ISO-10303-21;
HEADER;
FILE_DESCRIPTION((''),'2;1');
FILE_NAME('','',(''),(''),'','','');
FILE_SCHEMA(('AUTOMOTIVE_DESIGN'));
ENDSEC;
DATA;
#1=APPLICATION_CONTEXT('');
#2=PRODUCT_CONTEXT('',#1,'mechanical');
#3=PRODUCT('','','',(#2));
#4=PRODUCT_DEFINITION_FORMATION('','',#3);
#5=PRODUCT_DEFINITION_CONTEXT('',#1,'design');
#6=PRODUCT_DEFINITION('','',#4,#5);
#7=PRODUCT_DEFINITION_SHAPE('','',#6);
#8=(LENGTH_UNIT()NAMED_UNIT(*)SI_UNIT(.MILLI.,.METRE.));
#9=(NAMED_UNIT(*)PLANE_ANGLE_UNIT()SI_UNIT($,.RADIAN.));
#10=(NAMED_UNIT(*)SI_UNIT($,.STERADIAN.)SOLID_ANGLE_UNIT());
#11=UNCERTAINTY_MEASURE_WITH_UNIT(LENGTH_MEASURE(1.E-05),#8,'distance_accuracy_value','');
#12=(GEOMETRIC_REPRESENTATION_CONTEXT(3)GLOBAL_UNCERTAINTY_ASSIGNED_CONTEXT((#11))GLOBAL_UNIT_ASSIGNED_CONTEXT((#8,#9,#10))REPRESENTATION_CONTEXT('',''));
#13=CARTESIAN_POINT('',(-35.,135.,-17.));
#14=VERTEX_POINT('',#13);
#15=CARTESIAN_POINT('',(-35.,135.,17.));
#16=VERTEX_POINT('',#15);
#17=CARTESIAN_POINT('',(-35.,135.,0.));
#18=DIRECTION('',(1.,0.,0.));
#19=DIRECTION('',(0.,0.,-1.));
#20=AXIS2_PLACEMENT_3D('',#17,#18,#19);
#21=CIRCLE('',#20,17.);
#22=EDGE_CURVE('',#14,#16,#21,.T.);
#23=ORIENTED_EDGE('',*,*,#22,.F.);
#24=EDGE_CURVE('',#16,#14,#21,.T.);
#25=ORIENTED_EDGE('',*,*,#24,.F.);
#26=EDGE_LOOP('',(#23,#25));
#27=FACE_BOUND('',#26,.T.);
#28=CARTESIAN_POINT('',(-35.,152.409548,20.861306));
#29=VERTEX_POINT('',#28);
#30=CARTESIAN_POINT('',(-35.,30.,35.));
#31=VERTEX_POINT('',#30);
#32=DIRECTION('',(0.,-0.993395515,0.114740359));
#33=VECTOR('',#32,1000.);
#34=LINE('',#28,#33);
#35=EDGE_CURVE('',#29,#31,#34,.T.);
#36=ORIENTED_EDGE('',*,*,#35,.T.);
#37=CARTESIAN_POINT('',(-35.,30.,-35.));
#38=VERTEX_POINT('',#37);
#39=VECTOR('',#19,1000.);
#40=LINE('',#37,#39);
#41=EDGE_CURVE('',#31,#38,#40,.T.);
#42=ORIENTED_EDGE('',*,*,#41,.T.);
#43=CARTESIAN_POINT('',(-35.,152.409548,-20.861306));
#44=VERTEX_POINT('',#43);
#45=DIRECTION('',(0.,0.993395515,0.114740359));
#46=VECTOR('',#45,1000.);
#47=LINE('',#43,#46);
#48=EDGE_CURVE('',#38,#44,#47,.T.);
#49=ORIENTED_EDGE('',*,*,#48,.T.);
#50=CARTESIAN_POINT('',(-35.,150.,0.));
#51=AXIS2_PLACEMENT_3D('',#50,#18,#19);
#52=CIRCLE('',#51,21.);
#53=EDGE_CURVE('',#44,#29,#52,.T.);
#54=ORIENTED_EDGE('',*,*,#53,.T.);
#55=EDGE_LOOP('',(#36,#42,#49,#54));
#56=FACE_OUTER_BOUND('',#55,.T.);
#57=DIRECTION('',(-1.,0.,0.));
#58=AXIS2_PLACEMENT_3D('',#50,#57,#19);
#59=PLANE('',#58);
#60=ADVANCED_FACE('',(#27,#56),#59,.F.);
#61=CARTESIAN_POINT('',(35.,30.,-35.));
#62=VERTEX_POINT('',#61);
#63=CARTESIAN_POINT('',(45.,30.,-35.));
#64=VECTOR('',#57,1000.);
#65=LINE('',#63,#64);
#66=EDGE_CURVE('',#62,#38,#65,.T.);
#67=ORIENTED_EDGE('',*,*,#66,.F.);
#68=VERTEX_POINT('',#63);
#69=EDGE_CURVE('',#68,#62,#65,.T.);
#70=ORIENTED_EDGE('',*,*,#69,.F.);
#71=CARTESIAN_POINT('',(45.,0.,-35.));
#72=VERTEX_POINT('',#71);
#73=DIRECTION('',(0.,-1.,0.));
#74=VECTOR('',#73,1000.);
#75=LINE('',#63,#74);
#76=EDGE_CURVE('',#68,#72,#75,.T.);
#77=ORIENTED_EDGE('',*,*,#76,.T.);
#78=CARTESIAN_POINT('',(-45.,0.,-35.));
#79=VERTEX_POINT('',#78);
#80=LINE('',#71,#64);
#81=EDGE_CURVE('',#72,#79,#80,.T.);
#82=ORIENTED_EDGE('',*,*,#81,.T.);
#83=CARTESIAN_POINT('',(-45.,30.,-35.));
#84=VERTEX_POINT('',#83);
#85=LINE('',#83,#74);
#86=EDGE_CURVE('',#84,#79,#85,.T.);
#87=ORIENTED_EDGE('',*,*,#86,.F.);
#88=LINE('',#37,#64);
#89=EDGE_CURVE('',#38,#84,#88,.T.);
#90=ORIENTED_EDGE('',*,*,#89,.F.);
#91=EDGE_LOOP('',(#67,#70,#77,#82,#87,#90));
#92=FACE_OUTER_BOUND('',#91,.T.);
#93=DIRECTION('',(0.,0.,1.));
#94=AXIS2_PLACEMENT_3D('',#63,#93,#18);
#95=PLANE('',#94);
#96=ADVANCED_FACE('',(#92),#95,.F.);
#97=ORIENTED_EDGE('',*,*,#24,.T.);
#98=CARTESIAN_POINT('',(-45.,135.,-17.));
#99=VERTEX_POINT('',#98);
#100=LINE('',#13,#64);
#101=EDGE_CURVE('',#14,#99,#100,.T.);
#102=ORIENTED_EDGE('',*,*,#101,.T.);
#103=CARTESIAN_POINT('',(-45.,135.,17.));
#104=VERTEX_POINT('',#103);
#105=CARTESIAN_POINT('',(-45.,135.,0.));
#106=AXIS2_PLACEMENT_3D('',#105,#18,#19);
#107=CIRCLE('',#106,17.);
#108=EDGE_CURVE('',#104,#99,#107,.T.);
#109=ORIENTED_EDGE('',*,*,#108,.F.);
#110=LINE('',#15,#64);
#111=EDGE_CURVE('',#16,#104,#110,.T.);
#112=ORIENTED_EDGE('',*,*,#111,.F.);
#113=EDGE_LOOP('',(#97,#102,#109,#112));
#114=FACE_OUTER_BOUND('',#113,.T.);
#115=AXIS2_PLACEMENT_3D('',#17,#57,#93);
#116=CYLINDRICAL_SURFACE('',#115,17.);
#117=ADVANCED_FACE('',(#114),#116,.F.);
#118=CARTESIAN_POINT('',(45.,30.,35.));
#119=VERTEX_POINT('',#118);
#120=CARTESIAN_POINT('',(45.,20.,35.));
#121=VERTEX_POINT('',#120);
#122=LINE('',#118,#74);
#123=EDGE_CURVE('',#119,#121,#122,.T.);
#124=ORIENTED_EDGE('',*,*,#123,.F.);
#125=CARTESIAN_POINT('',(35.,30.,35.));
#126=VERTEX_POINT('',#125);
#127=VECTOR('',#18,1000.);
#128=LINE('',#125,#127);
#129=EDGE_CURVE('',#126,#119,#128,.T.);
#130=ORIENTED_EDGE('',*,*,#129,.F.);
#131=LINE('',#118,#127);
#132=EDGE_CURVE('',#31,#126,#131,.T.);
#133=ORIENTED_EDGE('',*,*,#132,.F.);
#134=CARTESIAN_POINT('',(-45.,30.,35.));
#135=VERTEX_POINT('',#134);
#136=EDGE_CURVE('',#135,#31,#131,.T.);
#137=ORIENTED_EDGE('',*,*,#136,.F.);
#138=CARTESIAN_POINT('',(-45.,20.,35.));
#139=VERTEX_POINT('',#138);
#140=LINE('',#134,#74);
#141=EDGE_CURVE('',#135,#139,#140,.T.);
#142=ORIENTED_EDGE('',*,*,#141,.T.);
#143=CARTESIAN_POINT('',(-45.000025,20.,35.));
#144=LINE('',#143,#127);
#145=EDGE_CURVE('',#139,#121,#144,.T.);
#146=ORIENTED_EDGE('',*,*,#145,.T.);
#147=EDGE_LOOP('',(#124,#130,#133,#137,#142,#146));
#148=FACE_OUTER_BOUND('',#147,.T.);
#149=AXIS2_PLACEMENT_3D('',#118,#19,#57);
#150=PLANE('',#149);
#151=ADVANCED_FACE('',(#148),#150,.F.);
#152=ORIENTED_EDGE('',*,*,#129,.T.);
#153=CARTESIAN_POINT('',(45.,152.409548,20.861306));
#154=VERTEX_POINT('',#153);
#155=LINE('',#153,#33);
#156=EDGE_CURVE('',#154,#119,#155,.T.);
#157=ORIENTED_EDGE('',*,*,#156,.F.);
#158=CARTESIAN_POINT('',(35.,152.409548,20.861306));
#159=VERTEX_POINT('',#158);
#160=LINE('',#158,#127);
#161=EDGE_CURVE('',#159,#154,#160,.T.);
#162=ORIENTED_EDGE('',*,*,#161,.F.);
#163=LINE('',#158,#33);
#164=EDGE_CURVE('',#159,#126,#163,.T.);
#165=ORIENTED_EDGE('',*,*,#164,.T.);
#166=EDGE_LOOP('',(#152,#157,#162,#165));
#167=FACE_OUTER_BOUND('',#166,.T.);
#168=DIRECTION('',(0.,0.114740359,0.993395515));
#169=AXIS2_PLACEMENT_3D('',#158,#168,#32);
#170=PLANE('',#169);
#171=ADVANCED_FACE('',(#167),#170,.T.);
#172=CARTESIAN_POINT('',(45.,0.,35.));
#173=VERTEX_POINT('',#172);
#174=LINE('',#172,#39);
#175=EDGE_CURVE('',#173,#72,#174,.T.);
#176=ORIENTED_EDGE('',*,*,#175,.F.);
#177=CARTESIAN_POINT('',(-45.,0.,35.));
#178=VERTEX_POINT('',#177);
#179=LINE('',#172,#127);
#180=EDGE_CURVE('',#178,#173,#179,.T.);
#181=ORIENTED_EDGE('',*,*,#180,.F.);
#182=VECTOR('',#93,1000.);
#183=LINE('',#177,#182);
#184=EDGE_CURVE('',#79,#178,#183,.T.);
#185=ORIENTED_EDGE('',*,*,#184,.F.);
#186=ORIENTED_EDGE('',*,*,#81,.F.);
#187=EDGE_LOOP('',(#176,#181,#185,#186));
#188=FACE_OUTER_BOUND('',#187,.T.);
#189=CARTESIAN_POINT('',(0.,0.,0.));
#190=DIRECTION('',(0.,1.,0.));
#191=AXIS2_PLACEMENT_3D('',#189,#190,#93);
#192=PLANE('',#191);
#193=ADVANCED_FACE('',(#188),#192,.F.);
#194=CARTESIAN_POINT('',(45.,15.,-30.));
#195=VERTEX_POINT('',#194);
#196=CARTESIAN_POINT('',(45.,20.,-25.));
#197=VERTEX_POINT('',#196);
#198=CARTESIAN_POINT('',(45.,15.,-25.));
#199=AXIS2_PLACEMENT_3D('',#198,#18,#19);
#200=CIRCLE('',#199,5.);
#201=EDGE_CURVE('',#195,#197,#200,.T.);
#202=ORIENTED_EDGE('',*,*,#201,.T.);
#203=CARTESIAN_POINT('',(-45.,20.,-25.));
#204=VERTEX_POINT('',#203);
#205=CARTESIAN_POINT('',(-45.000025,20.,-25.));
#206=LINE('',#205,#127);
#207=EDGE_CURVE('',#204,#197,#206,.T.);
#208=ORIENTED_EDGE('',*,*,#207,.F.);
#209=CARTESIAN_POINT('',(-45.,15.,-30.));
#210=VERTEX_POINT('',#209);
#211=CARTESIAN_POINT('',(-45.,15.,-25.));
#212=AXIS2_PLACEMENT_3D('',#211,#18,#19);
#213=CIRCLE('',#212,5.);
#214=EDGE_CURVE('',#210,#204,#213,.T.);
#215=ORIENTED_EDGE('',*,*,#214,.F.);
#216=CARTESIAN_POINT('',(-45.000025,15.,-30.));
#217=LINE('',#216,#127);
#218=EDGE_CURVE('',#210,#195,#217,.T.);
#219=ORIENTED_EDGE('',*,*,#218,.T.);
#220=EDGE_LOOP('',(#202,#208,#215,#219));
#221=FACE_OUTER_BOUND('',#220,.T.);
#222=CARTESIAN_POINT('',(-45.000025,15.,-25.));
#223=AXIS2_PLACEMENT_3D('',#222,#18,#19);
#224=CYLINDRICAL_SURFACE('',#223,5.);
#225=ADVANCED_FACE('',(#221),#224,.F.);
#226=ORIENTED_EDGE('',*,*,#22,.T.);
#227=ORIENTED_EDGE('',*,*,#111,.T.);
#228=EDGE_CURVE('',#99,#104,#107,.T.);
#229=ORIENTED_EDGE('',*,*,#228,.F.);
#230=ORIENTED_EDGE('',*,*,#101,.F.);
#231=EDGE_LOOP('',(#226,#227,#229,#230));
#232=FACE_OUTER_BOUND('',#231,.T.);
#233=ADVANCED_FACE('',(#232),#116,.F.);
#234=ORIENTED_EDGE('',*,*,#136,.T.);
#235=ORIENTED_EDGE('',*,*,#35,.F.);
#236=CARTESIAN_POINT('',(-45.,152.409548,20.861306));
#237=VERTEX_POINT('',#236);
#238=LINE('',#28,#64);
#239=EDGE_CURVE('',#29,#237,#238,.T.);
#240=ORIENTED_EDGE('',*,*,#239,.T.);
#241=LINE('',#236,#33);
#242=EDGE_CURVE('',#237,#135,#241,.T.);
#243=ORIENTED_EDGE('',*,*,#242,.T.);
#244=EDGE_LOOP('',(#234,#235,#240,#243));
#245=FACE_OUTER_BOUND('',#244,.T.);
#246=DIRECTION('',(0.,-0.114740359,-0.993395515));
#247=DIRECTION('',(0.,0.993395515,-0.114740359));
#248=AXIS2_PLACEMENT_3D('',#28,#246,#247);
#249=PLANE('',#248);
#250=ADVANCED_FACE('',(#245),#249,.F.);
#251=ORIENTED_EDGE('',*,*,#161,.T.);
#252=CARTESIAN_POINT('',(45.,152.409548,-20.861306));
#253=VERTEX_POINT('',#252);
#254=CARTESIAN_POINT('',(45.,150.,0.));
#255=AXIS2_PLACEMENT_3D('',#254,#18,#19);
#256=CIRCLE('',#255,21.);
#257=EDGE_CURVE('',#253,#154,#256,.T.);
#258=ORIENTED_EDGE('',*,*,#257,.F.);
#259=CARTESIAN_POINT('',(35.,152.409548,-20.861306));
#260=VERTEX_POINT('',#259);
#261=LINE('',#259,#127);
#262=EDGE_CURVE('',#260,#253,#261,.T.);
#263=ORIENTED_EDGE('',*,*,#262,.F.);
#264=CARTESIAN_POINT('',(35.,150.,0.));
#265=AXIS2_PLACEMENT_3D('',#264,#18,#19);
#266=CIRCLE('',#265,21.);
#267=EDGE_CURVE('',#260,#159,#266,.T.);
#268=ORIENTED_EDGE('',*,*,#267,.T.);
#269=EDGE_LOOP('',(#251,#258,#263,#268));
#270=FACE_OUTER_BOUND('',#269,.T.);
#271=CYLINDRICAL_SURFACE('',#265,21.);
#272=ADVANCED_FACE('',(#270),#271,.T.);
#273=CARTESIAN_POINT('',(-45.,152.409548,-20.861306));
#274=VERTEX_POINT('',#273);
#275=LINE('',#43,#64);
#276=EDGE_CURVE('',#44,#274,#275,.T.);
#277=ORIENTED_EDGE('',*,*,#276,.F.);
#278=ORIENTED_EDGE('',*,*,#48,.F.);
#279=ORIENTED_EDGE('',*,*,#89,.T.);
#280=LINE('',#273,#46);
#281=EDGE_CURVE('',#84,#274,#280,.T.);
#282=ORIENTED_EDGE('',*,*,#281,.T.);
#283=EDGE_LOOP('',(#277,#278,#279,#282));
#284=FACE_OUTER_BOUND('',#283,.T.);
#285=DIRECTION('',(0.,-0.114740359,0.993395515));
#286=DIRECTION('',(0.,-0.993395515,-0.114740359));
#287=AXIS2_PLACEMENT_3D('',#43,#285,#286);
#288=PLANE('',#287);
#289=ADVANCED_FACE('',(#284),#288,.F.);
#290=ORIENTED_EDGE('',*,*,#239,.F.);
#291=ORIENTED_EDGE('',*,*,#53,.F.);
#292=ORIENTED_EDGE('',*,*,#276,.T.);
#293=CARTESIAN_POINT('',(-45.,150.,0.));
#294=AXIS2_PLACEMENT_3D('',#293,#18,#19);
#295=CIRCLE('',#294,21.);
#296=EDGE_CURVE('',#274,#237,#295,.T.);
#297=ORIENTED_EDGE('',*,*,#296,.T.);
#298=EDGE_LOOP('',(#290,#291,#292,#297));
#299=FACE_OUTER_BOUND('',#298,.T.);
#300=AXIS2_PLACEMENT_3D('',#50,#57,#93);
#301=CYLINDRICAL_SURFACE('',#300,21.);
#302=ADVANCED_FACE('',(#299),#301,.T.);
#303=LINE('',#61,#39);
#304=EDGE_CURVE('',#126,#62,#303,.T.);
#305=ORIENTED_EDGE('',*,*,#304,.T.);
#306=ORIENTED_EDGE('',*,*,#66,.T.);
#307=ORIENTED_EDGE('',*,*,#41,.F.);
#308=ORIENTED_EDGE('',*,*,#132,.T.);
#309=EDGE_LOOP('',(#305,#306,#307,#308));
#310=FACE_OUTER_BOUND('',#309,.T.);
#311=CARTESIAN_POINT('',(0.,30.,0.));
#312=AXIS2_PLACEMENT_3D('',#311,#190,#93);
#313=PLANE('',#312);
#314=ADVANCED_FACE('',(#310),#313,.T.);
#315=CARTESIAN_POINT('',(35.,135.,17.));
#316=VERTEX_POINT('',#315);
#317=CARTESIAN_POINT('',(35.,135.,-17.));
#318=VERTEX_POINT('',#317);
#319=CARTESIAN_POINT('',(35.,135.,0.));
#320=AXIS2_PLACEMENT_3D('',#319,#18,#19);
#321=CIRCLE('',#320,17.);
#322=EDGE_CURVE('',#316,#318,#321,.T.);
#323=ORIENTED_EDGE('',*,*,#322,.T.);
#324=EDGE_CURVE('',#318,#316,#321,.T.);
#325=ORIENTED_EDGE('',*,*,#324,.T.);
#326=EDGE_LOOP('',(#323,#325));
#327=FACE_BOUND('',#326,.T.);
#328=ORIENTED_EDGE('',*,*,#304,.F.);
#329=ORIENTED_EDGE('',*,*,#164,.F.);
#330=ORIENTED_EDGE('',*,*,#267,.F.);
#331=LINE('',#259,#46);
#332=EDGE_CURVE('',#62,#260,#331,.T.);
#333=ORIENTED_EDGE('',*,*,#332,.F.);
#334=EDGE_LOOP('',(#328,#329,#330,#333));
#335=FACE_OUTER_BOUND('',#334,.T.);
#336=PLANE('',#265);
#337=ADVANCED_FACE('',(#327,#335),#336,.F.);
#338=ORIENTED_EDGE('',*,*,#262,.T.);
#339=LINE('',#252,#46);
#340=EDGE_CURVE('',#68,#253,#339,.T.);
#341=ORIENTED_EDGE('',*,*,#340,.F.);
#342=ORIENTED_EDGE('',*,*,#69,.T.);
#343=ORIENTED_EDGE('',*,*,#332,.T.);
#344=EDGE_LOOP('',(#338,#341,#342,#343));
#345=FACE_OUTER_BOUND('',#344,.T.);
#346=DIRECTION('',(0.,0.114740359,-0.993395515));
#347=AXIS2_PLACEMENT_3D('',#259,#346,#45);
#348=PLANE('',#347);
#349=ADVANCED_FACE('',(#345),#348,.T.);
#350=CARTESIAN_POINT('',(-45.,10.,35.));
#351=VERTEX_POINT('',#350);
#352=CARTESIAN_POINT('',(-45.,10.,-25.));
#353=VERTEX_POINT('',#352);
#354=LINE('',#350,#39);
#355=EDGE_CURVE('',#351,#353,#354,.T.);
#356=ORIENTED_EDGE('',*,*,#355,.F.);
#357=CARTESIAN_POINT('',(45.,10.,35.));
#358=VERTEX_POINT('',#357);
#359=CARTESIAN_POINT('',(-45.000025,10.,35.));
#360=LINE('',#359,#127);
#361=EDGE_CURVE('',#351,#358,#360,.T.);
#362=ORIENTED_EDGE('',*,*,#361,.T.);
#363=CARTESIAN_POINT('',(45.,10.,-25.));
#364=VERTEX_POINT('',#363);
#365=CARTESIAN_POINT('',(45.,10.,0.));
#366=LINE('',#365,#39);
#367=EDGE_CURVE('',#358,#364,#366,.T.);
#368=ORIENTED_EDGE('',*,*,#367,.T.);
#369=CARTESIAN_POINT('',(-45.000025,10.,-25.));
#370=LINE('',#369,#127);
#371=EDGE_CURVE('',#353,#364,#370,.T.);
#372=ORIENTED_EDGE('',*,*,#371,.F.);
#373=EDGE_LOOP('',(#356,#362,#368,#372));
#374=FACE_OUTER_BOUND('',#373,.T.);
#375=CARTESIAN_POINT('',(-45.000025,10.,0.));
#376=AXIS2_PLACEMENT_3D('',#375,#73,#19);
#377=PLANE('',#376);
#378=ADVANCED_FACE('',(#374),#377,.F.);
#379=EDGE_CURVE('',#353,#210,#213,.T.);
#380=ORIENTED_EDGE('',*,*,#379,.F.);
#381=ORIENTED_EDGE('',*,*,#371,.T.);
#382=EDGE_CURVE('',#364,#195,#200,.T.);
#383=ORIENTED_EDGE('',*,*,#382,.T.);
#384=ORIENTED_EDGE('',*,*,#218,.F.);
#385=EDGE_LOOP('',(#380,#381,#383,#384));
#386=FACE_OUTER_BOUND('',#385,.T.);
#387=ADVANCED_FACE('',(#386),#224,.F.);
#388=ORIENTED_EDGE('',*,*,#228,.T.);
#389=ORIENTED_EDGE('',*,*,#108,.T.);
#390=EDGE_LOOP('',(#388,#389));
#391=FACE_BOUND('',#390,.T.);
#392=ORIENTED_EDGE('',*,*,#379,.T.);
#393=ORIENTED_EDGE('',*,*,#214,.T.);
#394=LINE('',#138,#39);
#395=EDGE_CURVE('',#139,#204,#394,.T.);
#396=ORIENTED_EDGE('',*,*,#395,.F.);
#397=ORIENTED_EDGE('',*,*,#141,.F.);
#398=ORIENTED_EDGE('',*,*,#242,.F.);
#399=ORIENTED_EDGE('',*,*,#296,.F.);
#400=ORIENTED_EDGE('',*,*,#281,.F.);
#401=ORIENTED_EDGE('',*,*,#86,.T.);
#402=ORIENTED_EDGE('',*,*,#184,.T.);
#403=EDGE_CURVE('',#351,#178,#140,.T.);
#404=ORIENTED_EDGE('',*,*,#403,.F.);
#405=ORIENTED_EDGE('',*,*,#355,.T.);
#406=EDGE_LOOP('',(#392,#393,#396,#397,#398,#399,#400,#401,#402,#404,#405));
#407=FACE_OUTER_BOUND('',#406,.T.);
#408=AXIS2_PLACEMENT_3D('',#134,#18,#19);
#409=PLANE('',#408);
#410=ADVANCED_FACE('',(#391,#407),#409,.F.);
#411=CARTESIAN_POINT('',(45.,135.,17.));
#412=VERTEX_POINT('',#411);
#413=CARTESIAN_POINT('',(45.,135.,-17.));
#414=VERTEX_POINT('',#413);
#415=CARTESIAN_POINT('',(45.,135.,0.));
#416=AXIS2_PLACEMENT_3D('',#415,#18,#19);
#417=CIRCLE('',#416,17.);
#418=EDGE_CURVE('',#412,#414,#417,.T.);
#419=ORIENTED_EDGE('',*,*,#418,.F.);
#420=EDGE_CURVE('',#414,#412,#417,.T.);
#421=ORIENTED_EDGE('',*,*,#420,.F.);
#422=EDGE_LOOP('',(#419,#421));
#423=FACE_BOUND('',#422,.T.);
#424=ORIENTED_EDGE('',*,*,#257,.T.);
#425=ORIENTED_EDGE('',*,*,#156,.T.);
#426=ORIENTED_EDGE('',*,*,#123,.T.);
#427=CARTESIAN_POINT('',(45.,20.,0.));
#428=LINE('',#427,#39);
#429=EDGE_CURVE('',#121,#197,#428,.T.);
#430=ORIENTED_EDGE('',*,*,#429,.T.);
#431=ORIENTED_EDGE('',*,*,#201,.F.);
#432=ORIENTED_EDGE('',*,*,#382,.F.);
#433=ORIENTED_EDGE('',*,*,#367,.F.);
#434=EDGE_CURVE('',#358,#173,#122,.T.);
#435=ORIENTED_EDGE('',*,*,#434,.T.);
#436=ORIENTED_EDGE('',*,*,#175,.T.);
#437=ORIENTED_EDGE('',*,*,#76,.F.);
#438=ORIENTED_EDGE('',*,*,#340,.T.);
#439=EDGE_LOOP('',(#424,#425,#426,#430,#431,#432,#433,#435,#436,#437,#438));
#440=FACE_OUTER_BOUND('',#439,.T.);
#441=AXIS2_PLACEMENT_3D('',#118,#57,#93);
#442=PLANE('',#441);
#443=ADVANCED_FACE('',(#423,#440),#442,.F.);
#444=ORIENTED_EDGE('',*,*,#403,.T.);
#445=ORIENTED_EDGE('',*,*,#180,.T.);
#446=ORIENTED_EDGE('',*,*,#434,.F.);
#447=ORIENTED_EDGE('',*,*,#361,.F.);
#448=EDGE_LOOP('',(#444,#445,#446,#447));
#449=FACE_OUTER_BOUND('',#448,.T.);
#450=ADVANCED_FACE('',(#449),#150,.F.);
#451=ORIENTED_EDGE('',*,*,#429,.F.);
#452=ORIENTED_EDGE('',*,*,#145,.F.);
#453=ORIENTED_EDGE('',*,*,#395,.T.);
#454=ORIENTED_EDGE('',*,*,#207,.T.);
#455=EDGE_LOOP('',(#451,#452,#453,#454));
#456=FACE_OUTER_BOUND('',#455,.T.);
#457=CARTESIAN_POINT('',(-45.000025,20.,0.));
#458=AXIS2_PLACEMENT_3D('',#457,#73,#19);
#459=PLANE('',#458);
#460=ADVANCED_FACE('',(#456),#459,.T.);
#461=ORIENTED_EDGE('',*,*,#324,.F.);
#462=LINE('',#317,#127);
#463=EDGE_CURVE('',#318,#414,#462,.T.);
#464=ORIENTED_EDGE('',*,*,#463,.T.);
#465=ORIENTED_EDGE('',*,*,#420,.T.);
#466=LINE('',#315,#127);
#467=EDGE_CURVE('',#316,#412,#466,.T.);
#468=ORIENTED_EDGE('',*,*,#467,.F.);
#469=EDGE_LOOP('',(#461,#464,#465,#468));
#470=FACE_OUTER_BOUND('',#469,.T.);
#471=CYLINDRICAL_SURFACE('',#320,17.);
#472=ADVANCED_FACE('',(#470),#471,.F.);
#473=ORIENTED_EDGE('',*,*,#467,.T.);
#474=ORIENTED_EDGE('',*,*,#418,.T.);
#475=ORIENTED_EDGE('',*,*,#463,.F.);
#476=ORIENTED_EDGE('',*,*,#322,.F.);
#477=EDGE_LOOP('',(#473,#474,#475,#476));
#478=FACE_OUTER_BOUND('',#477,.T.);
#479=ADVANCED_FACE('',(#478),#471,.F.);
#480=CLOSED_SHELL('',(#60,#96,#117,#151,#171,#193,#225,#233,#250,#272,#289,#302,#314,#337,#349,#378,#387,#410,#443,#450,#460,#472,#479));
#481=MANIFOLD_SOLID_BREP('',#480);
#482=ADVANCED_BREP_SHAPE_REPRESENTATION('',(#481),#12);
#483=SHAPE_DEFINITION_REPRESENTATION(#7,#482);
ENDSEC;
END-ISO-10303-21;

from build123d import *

# Parameters (mm, degrees)
SKETCH1_W           = 90
SKETCH1_H           = 70
BOSS_EXTRUDE1_DEPTH = 30
SKETCH2_R           = 17
BOSS_EXTRUDE2_DEPTH = 10
CUT_EXTRUDE1_DEPTH  = 197.38228026


with BuildPart() as part:
    # Sketch1 → Boss-Extrude1 (new body)
    with BuildSketch(Plane(origin=(0, 0, 0), x_dir=(1, 0, 0), z_dir=(0, 1, 0))):
        Rectangle(SKETCH1_W, SKETCH1_H)
    extrude(amount=BOSS_EXTRUDE1_DEPTH)

    # Sketch2 → Boss-Extrude2 (add)
    with BuildSketch(Plane(origin=(45, 0, 0), x_dir=(0, 0, -1), z_dir=(1, 0, 0))):
        with BuildLine():
            Line((-20.861305824, 152.409547532), (-35, 30))
            Line((-35, 30), (35, 30))
            Line((35, 30), (20.861305824, 152.409547532))
            ThreePointArc((20.861305824, 152.409547532), (0, 171), (-20.861305824, 152.409547532))
        make_face()
        with Locations((0, 135)):
            Circle(SKETCH2_R, mode=Mode.SUBTRACT)
    boss_extrude2 = extrude(amount=-BOSS_EXTRUDE2_DEPTH)

    # Mirror1: Boss-Extrude2 across plane
    add(boss_extrude2.mirror(Plane(origin=(0, 0, 0), x_dir=(0, 0, 1), z_dir=(1, 0, 0))))

    # Sketch3 → Cut-Extrude1 (cut, through all)
    with BuildSketch(Plane(origin=(45, 0, 0), x_dir=(0, 0, -1), z_dir=(1, 0, 0))):
        with BuildLine():
            Line((25, 20), (-35, 20))
            Line((-35, 20), (-35, 10))
            Line((-35, 10), (25, 10))
            ThreePointArc((25, 10), (20, 15), (25, 20))
        make_face()
        with BuildLine():
            ThreePointArc((30, 15), (28.535533906, 18.535533906), (25, 20))
            Line((25, 20), (25, 10))
            ThreePointArc((25, 10), (28.535533906, 11.464466094), (30, 15))
        make_face()
        with BuildLine():
            Line((25, 10), (25, 20))
            ThreePointArc((25, 20), (20, 15), (25, 10))
        make_face()
    extrude(amount=-CUT_EXTRUDE1_DEPTH, mode=Mode.SUBTRACT)


solid = part.part
